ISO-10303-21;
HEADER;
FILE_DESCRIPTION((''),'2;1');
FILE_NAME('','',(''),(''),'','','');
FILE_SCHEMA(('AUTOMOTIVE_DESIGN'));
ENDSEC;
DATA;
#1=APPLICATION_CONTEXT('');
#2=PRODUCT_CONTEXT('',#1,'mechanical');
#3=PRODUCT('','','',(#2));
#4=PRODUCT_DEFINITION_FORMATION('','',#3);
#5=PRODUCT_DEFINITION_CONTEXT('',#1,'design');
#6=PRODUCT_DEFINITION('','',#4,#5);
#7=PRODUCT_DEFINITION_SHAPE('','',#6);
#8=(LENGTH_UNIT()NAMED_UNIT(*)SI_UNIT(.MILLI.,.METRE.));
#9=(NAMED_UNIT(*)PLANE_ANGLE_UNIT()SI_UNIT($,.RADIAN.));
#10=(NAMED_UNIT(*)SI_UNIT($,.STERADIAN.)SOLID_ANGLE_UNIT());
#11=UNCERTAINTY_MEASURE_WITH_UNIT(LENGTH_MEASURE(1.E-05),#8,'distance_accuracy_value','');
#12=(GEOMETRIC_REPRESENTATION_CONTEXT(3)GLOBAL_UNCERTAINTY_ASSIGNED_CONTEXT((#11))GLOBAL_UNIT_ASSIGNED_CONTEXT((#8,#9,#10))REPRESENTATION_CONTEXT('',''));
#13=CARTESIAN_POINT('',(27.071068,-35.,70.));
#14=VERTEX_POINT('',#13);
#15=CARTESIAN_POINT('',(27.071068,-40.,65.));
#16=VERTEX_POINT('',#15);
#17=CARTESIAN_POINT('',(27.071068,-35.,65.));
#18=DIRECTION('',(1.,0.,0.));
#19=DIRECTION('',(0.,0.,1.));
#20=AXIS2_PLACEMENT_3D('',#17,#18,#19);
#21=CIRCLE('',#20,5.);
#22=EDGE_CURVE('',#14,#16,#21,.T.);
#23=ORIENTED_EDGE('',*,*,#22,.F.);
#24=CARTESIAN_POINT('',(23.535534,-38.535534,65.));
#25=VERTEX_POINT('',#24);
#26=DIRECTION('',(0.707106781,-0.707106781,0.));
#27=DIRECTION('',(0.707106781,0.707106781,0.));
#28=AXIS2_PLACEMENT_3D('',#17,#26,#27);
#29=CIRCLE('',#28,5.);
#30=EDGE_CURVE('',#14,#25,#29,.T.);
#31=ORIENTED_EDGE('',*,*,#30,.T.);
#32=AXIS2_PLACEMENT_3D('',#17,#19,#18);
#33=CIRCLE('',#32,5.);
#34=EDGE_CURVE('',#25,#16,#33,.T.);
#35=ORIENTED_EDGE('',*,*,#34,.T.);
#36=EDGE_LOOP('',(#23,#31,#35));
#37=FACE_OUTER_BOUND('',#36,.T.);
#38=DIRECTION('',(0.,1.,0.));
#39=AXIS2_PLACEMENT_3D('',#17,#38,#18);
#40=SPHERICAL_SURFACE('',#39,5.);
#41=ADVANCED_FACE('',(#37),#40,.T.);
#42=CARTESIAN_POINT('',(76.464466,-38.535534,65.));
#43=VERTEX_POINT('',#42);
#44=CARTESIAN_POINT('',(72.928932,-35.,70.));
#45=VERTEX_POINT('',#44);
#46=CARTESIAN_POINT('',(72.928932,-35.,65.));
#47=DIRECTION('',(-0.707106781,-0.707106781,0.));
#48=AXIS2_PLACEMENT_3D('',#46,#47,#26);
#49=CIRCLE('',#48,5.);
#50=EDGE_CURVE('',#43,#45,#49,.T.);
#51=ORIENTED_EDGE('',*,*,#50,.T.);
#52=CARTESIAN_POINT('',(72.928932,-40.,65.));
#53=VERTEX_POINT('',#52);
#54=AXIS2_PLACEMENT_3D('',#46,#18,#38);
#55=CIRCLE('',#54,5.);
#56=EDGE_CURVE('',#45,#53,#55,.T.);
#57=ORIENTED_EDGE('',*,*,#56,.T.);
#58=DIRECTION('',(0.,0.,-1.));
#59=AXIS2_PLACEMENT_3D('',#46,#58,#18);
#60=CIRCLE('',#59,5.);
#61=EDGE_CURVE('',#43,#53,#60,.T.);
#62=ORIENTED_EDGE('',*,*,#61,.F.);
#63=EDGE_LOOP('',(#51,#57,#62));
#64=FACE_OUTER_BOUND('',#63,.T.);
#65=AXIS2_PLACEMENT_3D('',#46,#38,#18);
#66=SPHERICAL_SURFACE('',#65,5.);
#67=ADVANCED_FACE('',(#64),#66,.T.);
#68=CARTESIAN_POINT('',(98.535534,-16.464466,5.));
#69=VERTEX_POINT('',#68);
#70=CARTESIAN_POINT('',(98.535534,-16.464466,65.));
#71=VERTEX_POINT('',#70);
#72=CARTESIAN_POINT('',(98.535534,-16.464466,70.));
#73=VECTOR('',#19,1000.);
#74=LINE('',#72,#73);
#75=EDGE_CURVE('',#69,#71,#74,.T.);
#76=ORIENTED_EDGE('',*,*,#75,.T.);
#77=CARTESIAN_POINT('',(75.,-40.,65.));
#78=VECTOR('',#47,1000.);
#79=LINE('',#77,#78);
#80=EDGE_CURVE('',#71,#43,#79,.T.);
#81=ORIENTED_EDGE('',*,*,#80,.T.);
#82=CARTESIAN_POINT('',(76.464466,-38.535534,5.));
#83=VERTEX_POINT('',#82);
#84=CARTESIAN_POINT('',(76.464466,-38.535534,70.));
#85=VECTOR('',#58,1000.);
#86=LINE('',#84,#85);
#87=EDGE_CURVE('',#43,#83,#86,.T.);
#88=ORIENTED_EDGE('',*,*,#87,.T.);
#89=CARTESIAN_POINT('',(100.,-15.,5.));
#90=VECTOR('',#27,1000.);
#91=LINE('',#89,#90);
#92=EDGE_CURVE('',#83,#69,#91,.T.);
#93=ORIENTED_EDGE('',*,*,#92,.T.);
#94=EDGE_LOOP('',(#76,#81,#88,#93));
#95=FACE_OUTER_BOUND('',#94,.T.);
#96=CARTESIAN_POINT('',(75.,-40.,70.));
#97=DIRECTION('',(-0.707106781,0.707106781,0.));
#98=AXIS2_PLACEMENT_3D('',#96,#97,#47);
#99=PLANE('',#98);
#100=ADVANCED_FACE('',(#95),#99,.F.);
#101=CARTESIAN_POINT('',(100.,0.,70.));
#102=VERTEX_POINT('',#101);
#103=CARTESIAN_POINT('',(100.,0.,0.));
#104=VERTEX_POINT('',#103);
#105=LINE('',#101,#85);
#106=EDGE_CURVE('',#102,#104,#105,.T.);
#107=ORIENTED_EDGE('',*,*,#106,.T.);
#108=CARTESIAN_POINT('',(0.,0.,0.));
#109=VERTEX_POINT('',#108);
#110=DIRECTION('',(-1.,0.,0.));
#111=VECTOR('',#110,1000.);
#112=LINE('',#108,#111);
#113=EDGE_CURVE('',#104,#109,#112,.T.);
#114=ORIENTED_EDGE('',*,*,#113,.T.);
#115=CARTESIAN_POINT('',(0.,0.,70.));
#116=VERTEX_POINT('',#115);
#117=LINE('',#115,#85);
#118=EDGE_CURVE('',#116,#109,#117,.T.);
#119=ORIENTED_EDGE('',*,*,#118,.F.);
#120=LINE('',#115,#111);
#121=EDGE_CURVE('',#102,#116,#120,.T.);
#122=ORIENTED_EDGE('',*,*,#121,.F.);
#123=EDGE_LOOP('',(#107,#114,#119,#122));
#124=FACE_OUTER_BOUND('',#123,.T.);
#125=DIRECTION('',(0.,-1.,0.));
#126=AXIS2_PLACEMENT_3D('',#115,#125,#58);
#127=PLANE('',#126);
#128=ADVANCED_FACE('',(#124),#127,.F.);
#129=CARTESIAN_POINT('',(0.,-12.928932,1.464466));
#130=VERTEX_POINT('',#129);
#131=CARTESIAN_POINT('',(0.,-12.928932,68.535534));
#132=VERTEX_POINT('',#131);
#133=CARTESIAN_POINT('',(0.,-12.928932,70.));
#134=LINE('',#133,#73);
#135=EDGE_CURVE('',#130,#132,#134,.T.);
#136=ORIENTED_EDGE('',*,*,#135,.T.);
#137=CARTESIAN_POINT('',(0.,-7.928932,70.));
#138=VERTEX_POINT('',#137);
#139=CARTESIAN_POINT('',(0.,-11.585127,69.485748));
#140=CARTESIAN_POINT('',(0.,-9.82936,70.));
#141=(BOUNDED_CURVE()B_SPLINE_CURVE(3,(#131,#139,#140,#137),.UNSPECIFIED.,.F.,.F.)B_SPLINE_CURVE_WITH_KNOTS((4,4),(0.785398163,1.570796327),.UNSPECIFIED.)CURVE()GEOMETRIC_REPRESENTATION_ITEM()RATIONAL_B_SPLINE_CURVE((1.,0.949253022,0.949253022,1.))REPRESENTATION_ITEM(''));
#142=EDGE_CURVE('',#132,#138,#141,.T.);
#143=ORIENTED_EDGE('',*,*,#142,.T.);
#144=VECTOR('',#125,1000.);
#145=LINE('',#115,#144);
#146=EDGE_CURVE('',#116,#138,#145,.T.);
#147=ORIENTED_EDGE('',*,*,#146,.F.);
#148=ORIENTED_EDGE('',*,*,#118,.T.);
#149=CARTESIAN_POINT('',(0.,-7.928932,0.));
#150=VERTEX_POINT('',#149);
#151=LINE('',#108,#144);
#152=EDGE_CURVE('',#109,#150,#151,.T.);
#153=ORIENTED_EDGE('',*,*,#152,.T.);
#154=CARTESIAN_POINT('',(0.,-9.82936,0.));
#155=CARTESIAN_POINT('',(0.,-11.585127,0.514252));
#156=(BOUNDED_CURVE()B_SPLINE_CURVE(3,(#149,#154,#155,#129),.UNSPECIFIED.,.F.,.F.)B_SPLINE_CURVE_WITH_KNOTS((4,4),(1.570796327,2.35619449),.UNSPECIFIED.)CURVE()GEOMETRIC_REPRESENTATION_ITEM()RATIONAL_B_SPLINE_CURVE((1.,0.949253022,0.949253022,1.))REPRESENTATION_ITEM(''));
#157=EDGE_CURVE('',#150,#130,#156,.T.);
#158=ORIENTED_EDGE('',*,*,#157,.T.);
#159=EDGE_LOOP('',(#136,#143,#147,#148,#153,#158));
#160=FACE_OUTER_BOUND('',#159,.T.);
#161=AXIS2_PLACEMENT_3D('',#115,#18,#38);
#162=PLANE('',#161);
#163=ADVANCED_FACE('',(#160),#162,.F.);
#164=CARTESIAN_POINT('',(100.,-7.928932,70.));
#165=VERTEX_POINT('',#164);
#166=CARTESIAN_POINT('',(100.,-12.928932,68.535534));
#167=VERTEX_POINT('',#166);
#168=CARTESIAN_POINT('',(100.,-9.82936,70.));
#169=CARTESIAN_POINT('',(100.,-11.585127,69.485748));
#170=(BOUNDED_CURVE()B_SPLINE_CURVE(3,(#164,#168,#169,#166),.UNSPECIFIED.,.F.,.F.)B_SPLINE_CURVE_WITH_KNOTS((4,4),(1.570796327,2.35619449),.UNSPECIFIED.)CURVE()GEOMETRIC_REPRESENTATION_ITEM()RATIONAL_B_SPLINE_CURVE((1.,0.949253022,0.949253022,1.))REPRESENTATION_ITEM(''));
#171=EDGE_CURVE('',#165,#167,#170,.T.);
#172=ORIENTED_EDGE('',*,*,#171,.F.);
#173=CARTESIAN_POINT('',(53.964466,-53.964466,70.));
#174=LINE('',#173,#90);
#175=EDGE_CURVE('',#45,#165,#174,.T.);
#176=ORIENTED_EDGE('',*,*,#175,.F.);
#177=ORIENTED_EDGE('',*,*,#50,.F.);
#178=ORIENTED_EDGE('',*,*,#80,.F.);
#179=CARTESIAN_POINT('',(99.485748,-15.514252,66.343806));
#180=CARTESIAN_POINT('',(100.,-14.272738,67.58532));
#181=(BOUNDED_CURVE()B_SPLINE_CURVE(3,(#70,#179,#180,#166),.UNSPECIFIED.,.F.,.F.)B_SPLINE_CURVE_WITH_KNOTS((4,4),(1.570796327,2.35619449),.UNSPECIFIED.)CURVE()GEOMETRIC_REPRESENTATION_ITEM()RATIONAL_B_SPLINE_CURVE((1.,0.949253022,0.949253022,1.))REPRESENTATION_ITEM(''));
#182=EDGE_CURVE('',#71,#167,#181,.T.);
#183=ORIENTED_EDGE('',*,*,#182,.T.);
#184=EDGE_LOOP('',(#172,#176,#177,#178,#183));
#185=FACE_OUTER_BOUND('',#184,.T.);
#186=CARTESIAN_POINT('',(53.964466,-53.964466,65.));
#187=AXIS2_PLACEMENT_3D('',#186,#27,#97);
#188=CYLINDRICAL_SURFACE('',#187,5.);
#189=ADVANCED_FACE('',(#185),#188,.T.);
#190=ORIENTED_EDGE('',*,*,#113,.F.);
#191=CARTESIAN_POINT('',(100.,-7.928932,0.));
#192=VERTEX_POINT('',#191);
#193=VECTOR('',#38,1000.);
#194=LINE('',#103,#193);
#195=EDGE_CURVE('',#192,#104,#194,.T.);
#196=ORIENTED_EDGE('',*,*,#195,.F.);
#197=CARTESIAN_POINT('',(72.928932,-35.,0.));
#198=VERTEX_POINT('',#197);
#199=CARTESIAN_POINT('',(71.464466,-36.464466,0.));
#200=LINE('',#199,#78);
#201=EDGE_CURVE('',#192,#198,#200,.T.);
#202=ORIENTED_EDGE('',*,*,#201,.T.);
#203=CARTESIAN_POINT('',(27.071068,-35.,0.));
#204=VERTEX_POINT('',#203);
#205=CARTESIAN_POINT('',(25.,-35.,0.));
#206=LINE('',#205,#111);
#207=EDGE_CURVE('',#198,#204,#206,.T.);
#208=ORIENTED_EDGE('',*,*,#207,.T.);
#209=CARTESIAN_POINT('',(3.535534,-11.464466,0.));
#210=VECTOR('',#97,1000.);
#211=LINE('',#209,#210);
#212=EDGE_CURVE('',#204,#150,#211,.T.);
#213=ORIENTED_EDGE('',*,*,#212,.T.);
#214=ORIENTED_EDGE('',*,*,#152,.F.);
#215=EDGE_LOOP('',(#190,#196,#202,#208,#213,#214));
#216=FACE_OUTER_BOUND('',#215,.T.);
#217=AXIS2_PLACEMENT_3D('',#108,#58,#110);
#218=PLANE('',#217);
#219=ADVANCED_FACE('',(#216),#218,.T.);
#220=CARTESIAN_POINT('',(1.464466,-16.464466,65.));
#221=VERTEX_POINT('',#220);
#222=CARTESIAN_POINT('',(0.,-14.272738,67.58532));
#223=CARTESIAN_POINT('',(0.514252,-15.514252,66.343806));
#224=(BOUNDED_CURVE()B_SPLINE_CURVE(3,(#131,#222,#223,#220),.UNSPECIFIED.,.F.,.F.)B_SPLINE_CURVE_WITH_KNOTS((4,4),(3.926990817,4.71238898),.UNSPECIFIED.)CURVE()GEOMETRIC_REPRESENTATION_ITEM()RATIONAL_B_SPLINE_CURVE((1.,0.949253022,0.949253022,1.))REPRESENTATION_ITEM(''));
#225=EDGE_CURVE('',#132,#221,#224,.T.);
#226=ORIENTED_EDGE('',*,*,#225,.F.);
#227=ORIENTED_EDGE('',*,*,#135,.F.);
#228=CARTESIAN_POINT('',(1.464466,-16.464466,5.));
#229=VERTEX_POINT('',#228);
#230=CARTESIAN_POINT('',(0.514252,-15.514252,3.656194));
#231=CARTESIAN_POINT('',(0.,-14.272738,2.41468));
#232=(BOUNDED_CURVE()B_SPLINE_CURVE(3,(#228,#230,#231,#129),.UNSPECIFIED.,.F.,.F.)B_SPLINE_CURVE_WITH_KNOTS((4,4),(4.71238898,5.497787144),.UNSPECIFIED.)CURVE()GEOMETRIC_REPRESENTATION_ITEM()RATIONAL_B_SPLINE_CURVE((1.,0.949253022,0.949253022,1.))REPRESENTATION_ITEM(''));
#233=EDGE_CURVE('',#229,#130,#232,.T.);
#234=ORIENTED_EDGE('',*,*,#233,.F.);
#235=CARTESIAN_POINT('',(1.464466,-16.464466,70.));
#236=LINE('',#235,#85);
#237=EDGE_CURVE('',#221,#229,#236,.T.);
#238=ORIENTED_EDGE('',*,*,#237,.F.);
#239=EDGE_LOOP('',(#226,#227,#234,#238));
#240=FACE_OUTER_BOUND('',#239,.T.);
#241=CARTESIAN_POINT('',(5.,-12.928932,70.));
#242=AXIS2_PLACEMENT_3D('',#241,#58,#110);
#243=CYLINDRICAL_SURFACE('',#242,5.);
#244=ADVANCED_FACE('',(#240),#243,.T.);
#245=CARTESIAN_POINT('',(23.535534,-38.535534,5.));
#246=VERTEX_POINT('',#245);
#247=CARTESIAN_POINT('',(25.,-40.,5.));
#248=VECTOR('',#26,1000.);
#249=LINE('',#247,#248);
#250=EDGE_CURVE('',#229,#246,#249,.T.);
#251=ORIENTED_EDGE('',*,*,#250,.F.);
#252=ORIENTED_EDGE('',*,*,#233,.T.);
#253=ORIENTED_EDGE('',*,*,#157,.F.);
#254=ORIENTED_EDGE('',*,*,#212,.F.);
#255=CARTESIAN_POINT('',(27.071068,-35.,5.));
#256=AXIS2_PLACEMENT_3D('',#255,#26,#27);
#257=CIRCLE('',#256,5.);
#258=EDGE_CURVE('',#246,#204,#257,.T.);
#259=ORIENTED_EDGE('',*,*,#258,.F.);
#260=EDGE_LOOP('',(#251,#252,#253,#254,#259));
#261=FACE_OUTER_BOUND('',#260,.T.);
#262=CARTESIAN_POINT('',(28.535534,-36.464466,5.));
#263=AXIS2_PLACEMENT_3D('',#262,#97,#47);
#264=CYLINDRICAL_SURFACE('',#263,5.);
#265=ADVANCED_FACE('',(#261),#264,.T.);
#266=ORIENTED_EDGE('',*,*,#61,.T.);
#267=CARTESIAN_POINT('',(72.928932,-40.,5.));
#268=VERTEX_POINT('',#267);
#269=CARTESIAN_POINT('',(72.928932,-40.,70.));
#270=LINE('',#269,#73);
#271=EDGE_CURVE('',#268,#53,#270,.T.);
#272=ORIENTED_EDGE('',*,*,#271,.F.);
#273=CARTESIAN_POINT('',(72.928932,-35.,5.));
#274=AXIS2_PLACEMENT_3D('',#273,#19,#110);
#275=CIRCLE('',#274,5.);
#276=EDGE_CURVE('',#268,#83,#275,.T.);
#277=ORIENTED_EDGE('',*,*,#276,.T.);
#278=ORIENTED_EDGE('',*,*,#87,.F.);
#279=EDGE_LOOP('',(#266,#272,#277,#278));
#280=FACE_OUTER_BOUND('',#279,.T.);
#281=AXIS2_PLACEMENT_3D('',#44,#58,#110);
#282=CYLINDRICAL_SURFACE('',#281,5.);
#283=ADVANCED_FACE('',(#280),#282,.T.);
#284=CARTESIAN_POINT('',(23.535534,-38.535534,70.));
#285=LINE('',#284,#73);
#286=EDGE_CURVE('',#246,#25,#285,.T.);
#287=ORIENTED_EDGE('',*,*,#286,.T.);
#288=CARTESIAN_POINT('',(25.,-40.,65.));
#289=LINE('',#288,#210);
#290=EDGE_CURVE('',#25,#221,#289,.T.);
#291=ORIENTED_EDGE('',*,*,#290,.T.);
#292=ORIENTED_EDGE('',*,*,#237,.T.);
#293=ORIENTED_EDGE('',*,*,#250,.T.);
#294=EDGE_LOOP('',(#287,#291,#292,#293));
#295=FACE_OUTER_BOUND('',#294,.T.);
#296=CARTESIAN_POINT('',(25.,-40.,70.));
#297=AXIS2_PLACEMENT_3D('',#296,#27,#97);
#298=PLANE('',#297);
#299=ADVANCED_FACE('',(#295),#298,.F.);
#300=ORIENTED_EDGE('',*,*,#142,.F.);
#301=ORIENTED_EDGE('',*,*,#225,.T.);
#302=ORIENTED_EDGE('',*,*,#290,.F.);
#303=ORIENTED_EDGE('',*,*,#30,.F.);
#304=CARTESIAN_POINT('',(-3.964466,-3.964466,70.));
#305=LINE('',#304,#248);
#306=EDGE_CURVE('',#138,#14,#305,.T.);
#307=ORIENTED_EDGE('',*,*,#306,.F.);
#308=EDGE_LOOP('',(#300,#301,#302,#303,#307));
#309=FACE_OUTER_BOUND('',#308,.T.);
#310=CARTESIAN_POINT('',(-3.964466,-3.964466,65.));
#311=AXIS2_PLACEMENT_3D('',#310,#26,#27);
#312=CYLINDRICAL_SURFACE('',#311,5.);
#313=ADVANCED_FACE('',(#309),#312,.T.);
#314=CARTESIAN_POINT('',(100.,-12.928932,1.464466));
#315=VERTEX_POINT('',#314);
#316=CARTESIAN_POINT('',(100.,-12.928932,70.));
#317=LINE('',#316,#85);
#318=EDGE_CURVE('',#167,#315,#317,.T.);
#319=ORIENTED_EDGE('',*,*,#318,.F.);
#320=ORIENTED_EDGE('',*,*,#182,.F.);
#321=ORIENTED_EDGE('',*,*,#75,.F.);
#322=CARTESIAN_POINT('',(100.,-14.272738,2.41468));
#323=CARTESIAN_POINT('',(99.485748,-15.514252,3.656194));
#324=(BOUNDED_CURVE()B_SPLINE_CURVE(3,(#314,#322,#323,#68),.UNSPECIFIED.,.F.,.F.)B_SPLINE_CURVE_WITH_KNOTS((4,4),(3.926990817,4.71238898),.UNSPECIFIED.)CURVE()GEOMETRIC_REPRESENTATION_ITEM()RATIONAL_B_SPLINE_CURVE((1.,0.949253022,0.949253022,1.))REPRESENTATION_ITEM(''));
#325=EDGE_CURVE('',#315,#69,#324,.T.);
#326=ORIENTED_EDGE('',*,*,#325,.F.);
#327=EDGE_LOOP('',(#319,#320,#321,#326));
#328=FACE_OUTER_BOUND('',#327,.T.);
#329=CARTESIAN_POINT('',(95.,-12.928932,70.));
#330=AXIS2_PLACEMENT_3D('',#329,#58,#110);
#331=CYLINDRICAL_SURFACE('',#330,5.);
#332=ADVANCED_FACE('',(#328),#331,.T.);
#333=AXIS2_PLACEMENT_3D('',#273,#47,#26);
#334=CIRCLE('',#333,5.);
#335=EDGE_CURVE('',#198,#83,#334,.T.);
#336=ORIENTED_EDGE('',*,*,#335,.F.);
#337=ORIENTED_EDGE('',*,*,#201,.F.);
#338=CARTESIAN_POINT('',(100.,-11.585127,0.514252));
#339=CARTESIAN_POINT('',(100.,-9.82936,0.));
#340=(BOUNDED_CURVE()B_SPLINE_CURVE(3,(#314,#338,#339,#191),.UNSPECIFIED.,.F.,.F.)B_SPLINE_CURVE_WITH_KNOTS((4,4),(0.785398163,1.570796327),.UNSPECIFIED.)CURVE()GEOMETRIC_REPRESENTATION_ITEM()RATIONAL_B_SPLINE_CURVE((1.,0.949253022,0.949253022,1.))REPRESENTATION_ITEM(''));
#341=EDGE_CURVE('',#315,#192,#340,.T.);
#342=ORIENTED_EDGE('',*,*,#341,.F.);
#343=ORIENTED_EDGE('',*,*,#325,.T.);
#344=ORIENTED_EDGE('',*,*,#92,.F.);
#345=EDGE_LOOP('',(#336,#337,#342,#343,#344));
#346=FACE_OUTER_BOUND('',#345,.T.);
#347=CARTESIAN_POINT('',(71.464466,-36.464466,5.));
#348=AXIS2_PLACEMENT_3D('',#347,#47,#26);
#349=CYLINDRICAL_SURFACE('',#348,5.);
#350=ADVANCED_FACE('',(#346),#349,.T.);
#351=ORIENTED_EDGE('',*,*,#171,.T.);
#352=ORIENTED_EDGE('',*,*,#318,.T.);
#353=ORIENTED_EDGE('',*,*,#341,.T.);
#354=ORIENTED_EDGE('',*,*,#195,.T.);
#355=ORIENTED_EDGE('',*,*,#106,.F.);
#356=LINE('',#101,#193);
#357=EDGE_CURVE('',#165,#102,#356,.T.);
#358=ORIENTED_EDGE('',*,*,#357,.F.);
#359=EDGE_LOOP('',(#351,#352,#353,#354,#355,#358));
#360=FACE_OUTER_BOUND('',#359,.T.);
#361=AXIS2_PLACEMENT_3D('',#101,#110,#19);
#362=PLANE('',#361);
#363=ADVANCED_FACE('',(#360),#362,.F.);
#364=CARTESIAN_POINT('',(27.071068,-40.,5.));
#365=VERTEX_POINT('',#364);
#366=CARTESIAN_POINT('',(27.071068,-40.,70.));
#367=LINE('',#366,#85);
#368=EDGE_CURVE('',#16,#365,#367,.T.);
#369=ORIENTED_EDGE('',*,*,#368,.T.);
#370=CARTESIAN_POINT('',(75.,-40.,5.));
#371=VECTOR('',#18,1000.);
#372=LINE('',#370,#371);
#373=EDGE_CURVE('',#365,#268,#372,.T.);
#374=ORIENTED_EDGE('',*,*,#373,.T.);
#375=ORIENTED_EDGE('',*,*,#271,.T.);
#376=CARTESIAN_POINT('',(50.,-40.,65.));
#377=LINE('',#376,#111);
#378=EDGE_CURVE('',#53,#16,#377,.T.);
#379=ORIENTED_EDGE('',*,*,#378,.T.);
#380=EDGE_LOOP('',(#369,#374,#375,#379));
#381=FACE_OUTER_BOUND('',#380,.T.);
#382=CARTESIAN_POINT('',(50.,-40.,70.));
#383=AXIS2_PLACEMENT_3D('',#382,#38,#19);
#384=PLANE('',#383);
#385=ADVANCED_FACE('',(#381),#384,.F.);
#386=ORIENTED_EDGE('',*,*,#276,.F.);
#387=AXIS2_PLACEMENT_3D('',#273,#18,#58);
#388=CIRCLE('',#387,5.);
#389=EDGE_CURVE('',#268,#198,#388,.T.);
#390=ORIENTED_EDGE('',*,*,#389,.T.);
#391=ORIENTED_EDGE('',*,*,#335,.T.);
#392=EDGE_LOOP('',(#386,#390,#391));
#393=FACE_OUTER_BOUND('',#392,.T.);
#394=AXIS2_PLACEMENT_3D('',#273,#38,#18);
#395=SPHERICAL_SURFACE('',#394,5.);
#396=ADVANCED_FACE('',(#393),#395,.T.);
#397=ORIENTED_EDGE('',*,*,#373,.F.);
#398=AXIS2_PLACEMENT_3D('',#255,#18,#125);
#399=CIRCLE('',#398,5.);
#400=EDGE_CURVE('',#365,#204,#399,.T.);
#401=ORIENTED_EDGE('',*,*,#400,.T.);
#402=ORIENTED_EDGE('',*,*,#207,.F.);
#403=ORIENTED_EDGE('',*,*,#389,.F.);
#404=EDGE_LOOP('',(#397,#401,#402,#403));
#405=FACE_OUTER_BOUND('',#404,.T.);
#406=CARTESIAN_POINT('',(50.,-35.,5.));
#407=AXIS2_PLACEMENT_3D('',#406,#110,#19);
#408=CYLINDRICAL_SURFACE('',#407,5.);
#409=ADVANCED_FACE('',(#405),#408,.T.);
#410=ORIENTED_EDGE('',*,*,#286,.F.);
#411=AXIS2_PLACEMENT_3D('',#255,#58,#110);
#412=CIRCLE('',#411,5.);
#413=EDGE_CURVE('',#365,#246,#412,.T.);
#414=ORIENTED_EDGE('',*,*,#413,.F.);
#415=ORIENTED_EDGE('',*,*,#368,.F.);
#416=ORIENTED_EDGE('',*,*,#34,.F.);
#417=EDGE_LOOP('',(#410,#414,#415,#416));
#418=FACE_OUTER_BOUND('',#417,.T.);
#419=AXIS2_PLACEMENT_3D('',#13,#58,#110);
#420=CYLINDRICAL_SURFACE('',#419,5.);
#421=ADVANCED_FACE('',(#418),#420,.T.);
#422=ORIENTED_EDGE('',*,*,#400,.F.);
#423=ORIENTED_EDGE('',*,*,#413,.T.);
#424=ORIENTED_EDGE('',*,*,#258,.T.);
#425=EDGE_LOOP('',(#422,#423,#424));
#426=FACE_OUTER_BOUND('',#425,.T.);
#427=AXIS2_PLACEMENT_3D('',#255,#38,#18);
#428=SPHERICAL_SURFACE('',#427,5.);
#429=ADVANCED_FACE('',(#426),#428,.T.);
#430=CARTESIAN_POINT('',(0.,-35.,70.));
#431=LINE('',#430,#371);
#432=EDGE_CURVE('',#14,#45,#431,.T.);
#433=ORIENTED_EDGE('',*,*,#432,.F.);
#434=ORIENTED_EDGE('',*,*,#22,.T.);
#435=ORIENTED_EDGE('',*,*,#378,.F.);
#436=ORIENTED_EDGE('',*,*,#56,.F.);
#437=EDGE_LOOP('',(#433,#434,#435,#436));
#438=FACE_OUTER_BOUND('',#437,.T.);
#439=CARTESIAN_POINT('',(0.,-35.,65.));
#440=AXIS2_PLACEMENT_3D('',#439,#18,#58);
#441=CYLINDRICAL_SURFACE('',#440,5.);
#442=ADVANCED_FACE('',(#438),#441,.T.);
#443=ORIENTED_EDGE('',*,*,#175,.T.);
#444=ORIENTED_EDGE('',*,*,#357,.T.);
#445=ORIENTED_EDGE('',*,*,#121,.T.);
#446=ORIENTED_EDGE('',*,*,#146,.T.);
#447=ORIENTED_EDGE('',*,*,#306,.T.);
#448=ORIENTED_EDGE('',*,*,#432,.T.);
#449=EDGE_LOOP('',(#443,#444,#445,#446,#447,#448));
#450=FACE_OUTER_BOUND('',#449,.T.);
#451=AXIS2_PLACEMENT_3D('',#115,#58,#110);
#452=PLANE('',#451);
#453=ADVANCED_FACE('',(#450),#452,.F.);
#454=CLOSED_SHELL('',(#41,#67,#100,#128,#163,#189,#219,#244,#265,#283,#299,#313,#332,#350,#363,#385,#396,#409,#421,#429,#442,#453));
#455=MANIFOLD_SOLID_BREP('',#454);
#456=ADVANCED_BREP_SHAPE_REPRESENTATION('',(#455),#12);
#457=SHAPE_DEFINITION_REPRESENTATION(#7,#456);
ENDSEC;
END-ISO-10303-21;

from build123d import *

# Parameters (mm, degrees)
EXTRUDE_1_DEPTH = 70
FILLET_1_R      = 5


with BuildPart() as part:
    # 草图1 → 凸台-拉伸1 (new body)
    with BuildSketch(Plane.XY):
        Polygon((0, 0), (100, 0), (100, -15), (75, -40), (50, -40), (25, -40), (0, -15), align=None)
    extrude(amount=EXTRUDE_1_DEPTH)

    # 圆角1
    fillet_1_edges = [part.edges().sort_by_distance(p)[0] for p in [
        (50, -40, 70),
        (100, -15, 35),
        (75, -40, 35),
        (25, -40, 35),
        (0, -15, 35),
        (87.5, -27.5, 70),
        (12.5, -27.5, 70),
        (87.5, -27.5, 0),
        (50, -40, 0),
        (12.5, -27.5, 0),
    ]]
    fillet(fillet_1_edges, radius=FILLET_1_R)


solid = part.part
